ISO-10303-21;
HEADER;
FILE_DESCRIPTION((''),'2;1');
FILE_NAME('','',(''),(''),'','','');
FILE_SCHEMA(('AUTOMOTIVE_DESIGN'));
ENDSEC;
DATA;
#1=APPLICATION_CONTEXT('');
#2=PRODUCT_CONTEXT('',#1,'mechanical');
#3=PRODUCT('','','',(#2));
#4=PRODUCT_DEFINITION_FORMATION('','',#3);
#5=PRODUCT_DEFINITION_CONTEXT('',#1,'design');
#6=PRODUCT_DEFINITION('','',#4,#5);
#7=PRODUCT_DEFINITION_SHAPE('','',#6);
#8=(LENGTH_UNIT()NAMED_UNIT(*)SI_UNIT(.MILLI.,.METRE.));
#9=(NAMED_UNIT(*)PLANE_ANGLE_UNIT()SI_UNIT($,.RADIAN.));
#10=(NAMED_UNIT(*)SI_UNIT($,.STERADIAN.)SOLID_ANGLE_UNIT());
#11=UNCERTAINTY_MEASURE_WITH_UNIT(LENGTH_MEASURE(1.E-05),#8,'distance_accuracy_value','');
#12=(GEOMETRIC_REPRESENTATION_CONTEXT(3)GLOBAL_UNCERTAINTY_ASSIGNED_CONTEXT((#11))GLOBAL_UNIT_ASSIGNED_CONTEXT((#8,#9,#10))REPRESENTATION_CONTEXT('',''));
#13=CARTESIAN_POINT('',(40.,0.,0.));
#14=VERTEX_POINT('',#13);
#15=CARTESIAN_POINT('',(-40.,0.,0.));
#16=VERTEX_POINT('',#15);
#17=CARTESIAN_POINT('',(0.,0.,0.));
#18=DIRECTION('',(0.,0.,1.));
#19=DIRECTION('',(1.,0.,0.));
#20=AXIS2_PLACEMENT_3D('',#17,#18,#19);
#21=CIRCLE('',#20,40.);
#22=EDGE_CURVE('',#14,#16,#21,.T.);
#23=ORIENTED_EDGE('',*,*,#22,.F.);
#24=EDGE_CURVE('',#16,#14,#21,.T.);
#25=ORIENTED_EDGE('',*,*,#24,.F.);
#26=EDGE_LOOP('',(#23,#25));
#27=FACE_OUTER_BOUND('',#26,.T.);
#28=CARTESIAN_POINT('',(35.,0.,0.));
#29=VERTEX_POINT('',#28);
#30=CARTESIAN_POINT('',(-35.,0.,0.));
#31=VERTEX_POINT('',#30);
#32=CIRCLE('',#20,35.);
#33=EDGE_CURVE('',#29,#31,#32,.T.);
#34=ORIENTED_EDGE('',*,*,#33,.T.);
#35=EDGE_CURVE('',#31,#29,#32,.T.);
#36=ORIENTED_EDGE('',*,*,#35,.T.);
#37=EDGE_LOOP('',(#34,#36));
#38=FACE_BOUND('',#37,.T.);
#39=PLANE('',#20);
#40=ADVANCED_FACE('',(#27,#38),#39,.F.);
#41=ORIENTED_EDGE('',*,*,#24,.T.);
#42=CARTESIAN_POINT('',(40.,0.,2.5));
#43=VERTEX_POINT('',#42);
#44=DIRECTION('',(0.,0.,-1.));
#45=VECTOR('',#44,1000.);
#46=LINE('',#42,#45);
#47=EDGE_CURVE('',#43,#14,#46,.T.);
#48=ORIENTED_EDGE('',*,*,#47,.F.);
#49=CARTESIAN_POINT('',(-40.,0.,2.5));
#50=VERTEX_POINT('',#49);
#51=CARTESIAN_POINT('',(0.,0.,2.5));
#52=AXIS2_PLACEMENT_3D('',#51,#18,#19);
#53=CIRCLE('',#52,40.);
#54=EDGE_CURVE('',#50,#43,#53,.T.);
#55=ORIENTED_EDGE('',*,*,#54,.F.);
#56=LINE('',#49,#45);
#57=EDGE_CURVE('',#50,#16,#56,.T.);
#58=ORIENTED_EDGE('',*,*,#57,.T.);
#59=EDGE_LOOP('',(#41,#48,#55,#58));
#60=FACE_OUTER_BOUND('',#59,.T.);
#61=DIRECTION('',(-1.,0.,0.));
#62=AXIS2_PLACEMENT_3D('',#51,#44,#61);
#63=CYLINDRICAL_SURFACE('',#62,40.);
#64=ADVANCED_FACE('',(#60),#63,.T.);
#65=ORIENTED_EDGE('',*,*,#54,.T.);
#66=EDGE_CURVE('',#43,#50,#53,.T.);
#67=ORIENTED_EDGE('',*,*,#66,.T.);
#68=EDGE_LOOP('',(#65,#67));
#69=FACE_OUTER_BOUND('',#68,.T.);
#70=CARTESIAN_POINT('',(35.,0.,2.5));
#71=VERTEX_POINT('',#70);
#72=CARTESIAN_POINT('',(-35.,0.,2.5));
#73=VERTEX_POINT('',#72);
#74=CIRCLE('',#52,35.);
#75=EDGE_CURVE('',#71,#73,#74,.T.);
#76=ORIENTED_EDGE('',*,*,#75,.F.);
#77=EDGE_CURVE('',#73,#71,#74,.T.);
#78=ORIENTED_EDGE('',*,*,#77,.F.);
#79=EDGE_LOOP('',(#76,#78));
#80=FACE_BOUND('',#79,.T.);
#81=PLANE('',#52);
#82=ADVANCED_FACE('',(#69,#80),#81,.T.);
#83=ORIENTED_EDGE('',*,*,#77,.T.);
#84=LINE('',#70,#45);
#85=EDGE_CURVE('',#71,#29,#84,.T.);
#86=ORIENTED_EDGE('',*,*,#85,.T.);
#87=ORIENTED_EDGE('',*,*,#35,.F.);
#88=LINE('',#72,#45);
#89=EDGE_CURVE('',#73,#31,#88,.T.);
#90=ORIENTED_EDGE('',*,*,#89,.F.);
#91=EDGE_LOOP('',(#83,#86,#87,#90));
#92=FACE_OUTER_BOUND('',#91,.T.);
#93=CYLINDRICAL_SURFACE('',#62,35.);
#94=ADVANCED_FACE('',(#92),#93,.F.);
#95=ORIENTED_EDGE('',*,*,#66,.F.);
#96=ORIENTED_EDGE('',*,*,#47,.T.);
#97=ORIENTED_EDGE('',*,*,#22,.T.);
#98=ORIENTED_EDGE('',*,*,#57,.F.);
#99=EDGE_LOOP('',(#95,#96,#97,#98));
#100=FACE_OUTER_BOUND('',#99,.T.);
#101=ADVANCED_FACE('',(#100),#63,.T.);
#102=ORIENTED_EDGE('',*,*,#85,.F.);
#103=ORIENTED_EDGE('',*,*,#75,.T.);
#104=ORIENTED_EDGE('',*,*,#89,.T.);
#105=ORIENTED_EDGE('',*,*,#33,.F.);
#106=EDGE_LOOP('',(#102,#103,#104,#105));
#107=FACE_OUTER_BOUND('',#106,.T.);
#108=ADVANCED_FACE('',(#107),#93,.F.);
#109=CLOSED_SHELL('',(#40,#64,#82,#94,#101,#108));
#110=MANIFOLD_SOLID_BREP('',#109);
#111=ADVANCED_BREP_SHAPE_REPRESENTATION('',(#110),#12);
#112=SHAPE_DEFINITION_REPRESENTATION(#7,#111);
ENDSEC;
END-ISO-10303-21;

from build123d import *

# Parameters (mm, degrees)
SKETCH_1_R      = 40
SKETCH_1_R_2    = 35
EXTRUDE_1_DEPTH = 2.5


with BuildPart() as part:
    # 草图1 → 凸台-拉伸1 (new body)
    with BuildSketch(Plane.XY):
        Circle(SKETCH_1_R)
        Circle(SKETCH_1_R_2, mode=Mode.SUBTRACT)
    extrude(amount=EXTRUDE_1_DEPTH)


solid = part.part
